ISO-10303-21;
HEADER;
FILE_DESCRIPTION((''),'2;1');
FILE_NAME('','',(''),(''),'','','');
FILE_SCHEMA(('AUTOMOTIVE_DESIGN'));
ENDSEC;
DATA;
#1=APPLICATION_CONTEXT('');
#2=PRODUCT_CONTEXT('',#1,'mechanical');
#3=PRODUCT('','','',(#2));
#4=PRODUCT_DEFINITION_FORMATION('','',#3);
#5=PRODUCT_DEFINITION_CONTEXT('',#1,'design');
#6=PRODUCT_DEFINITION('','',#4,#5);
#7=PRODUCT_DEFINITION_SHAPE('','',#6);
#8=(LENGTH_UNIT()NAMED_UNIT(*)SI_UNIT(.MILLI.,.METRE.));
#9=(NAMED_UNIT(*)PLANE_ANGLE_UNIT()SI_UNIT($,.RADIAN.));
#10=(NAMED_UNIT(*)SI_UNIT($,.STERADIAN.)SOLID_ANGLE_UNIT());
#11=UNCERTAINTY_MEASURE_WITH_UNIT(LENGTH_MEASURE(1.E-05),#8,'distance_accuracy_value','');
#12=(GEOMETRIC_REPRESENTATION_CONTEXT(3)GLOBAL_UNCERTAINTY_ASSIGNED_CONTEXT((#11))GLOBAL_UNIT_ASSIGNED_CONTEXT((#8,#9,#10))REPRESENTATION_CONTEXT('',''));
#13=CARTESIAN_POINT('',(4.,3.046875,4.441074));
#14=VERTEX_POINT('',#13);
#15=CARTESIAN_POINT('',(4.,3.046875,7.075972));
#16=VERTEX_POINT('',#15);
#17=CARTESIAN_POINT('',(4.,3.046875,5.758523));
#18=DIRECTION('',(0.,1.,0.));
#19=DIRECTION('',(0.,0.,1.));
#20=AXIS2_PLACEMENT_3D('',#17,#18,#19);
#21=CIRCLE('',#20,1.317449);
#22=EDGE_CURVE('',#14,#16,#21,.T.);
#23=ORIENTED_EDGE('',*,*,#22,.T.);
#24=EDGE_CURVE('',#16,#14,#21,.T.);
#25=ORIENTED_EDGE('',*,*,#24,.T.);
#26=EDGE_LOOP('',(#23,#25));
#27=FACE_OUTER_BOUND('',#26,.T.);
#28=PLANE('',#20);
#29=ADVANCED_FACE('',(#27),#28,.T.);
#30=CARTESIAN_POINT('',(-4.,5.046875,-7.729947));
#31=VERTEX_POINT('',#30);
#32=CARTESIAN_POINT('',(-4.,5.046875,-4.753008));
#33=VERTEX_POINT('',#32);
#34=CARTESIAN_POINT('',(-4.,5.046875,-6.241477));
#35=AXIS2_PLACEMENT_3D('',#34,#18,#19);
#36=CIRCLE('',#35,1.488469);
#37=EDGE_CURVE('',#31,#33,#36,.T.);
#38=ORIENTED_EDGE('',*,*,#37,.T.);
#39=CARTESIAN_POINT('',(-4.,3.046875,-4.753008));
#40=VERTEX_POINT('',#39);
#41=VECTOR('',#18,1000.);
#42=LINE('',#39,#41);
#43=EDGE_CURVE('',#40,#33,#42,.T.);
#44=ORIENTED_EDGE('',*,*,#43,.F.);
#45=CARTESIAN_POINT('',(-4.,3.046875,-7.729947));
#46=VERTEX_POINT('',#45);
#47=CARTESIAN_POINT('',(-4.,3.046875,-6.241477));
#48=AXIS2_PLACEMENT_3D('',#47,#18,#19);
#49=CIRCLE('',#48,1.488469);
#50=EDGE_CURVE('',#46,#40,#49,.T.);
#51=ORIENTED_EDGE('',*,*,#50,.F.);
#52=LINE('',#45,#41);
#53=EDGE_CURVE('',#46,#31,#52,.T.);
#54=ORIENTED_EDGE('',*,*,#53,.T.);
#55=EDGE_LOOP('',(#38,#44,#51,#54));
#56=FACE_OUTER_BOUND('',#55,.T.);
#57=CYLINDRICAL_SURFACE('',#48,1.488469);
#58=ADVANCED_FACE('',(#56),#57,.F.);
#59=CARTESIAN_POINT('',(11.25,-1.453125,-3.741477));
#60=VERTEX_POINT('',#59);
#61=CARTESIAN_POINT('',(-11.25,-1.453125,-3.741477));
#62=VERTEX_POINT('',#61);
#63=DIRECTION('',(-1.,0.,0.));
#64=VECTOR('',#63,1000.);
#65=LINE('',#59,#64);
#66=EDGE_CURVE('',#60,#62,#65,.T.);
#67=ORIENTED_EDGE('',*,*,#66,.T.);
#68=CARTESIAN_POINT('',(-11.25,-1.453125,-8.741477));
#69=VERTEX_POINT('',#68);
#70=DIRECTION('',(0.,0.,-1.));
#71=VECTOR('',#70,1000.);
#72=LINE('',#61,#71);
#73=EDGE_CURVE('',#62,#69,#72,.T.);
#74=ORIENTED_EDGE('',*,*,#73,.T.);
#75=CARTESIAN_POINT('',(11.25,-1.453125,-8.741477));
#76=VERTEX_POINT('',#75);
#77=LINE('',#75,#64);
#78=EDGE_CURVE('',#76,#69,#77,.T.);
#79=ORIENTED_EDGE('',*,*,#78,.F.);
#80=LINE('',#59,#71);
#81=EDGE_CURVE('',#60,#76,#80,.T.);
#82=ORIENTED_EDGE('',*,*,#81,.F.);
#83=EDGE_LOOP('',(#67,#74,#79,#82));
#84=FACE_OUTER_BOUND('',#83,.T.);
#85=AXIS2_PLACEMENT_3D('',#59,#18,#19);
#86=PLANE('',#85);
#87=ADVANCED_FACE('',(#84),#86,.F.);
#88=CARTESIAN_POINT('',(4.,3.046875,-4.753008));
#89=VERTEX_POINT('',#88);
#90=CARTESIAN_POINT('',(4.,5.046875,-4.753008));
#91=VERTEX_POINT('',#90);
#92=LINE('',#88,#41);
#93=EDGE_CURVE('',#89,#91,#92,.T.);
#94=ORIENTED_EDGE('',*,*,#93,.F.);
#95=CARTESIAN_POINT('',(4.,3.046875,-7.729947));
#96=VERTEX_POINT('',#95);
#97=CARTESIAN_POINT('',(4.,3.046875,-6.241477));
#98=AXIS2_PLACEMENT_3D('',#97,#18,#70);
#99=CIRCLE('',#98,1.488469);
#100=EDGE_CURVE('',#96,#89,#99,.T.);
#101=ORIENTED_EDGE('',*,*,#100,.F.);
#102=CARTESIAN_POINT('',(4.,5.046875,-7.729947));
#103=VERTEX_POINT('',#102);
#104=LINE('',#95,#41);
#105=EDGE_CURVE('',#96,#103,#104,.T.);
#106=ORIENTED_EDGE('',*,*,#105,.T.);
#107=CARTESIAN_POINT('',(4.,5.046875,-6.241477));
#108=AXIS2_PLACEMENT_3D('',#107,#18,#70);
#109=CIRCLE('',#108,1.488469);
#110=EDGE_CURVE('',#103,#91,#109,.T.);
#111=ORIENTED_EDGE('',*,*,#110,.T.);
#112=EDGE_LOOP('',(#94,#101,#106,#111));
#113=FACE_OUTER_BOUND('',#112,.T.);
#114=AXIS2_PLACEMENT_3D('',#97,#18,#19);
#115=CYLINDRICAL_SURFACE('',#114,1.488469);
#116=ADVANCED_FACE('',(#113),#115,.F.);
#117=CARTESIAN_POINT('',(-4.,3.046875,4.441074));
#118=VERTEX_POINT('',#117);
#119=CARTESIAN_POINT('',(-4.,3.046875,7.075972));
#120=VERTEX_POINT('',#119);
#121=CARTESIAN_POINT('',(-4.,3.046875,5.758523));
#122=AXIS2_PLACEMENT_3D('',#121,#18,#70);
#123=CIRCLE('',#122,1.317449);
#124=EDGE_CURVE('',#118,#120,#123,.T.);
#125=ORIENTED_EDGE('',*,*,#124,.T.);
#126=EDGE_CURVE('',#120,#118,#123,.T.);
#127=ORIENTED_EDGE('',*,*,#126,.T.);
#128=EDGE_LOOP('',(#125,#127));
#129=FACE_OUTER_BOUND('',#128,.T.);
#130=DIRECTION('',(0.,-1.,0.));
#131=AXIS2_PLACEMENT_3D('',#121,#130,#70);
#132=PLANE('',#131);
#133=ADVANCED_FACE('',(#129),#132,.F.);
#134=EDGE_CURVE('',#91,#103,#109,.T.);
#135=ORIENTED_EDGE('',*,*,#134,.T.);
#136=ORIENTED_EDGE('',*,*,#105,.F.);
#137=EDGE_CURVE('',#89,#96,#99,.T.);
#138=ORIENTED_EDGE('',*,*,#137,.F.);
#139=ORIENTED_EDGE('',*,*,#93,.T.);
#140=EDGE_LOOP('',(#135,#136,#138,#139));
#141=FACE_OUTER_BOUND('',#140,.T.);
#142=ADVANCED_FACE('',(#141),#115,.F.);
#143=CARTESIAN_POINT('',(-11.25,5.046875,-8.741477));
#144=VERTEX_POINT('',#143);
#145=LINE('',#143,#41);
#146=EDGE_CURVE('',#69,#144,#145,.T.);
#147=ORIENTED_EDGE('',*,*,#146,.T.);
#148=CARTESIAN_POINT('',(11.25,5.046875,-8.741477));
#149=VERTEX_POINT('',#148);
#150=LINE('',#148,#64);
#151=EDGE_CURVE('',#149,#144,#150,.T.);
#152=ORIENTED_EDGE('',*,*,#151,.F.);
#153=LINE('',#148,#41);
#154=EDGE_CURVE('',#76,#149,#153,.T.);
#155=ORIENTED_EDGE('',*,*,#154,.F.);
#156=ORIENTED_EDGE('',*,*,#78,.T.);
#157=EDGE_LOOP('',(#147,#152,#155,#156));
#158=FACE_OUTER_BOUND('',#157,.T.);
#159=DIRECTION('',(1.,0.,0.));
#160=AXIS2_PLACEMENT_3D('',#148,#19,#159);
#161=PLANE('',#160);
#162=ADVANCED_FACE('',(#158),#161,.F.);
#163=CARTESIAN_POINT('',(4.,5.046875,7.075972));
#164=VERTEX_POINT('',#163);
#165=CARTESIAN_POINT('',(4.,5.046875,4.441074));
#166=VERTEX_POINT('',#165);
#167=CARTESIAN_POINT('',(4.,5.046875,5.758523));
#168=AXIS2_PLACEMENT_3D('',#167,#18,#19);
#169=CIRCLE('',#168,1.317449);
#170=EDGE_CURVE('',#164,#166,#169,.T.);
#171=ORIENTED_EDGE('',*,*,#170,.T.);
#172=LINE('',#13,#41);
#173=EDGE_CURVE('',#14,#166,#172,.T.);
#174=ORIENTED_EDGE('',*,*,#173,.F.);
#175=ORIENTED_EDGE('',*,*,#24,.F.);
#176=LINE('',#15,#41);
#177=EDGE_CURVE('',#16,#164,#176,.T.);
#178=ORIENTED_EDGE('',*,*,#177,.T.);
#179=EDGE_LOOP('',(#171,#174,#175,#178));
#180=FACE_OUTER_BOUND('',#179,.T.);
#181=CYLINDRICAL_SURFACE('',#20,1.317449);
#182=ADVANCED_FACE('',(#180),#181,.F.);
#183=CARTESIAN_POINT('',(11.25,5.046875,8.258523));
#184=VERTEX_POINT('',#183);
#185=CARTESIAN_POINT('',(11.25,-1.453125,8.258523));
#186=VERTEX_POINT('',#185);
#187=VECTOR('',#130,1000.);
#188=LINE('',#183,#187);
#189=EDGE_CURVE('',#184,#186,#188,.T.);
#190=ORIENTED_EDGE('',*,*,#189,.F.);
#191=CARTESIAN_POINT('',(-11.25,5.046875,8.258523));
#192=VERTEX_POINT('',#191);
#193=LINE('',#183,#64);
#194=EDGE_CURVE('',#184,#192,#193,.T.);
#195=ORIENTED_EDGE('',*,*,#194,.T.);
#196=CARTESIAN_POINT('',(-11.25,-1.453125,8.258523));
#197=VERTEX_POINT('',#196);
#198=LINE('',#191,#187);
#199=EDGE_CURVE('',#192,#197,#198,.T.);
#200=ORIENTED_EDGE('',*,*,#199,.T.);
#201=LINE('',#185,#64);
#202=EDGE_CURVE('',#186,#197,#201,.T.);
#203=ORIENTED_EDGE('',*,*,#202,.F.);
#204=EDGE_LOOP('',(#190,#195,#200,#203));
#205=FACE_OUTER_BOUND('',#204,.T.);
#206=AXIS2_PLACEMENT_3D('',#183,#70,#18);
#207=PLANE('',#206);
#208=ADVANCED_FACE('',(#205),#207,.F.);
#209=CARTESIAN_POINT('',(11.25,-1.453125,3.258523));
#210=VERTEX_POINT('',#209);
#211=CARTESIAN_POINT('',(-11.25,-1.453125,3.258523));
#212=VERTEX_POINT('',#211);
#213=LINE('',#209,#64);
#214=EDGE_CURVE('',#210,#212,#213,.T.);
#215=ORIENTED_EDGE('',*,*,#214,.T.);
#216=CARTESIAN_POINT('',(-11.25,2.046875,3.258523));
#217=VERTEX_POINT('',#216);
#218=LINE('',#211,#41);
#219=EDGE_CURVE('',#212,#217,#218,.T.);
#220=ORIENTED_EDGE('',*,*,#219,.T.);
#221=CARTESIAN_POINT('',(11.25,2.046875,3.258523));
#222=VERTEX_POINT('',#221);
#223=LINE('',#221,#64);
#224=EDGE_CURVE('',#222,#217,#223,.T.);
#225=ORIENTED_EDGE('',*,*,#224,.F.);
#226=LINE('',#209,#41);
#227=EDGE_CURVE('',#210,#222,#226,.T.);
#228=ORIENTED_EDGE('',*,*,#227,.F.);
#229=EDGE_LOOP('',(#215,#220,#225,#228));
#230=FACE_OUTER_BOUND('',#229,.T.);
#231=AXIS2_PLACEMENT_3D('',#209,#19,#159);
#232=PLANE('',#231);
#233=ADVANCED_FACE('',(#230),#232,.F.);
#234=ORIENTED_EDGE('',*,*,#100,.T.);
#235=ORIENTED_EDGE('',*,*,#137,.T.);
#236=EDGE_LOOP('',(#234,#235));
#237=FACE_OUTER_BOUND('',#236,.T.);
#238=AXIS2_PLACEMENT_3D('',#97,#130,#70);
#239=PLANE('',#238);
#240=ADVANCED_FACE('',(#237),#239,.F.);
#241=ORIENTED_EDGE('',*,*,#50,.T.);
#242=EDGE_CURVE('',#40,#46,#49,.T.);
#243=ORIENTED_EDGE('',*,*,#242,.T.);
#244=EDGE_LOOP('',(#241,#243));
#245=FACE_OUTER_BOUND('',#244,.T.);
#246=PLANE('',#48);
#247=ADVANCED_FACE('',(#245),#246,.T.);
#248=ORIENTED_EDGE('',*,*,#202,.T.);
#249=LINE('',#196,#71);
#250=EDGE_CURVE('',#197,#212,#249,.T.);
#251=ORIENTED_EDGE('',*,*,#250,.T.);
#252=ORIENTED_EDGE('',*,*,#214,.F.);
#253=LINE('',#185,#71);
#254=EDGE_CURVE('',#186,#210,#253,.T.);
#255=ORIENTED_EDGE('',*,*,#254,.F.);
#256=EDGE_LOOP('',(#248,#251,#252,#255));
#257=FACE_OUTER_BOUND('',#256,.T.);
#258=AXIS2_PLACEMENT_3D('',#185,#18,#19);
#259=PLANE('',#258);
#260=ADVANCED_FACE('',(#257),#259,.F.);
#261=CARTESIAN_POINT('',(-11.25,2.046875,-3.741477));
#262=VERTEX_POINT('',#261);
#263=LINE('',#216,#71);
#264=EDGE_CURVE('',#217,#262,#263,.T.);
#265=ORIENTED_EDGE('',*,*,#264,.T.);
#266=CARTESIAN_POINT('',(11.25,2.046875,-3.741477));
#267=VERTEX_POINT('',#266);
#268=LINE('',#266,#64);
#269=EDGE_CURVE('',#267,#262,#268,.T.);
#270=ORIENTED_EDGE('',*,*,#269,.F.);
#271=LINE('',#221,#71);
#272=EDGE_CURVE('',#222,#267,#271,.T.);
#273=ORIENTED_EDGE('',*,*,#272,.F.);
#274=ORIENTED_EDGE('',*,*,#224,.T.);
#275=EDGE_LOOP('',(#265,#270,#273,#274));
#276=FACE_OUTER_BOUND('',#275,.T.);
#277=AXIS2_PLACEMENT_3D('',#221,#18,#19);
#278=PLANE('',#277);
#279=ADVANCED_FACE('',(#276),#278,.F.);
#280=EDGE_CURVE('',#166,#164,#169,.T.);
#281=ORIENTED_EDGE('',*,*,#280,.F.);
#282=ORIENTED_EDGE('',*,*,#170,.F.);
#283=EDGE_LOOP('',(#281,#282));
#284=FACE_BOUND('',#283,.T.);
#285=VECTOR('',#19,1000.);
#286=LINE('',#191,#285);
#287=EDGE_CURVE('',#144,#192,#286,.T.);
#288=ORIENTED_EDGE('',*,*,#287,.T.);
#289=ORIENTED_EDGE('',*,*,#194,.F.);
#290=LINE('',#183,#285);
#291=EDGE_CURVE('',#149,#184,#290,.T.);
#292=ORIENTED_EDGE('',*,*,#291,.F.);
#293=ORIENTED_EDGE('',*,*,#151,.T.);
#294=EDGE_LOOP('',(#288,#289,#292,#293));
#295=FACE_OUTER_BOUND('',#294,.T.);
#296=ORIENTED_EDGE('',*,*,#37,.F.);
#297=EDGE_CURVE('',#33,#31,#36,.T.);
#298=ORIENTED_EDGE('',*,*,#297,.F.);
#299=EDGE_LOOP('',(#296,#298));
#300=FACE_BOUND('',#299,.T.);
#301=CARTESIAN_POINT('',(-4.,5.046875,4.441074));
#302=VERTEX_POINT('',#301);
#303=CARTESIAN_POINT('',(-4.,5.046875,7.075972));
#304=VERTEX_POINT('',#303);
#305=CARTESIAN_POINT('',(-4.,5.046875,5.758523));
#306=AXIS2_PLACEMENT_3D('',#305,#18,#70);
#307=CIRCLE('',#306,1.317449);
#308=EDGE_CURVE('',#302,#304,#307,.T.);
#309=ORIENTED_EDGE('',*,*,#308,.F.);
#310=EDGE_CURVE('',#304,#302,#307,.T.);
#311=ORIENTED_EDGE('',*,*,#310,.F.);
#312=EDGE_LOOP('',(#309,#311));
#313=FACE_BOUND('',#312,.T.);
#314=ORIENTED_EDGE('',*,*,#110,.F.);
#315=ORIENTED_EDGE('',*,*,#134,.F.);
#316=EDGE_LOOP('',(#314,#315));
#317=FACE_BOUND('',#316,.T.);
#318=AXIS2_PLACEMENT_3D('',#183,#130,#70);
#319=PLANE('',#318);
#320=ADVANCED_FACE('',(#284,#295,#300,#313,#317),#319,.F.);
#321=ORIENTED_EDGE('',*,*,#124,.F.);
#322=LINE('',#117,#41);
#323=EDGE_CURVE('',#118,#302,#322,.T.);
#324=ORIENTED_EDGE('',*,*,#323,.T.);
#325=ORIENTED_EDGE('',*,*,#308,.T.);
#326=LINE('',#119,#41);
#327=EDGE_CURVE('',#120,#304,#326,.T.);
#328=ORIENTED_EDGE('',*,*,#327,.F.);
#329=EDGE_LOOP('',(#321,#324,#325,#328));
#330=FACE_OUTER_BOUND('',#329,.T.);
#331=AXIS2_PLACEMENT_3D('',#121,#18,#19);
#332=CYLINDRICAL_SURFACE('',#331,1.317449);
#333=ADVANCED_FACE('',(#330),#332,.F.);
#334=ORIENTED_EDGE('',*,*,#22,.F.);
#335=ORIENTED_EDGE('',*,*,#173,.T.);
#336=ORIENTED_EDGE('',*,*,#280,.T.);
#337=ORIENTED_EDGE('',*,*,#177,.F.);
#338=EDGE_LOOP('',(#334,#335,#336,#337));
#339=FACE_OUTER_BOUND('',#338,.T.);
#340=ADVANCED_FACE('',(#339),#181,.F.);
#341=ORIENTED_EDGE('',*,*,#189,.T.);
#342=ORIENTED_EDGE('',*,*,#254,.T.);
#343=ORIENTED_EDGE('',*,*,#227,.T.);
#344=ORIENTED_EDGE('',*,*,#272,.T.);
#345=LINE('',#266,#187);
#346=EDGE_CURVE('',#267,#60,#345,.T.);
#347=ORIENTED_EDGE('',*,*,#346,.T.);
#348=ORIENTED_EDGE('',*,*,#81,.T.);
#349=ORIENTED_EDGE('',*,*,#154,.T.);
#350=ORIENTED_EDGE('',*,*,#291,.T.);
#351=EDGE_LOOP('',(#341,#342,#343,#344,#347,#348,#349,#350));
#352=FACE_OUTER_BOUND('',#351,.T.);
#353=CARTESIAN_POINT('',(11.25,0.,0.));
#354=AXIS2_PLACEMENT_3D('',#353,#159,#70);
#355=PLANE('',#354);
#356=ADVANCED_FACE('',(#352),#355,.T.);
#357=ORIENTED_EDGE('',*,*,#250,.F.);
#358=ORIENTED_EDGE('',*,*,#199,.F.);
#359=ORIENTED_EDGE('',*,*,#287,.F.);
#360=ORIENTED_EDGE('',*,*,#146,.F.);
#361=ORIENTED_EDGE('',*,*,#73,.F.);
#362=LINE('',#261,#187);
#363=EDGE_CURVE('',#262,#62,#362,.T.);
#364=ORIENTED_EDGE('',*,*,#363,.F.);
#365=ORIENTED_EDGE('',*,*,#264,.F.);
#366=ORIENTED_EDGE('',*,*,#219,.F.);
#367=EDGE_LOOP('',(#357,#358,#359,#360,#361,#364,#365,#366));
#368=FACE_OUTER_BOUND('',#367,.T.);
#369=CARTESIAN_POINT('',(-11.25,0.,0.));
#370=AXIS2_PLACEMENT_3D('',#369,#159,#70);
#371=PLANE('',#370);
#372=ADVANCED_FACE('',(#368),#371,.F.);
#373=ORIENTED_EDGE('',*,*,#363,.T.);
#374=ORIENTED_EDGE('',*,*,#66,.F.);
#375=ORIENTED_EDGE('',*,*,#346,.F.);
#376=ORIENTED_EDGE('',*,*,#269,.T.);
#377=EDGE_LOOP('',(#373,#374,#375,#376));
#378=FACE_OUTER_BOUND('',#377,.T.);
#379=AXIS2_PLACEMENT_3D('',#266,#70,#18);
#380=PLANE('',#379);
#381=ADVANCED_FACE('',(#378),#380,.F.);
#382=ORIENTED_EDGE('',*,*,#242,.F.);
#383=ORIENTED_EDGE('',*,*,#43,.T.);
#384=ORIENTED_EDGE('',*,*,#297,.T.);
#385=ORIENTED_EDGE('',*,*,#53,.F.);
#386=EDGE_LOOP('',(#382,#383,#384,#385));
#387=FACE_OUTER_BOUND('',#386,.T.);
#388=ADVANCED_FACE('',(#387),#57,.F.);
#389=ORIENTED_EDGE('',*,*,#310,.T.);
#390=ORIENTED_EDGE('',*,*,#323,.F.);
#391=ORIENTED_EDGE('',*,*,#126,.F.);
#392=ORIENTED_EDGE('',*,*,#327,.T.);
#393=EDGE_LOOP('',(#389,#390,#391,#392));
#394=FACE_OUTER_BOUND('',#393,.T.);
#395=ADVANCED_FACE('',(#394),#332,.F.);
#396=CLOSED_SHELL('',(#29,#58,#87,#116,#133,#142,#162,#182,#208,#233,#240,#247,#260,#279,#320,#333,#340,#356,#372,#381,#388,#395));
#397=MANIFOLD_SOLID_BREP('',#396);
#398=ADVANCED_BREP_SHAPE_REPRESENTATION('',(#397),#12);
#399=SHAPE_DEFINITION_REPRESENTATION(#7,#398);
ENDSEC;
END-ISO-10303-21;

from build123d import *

# Parameters (mm, degrees)
BOSS_EXTRUDE1_DEPTH = 11.25
SKETCH2_R           = 1.317449136
SKETCH2_R_2         = 1.488469479
CUT_EXTRUDE1_DEPTH  = 2


with BuildPart() as part:
    # Sketch1 → Boss-Extrude1 (new, symmetric)
    with BuildSketch(Plane(origin=(0, 0, 0), x_dir=(0, 0, -1), z_dir=(1, 0, 0))):
        Polygon((-8.258522727, 5.046875), (8.741477273, 5.046875), (8.741477273, -1.453125), (3.741477273, -1.453125), (3.741477273, 2.046875), (-3.258522727, 2.046875), (-3.258522727, -1.453125), (-8.258522727, -1.453125), align=None)
    extrude(amount=BOSS_EXTRUDE1_DEPTH, both=True)

    # Sketch2 → Cut-Extrude1 (cut)
    with BuildSketch(Plane(origin=(0, 5.046875, 0), x_dir=(1, 0, 0), z_dir=(0, 1, 0))):
        with Locations(Location((4, -5.758522727, 0), (0, 0, 270))):
            Circle(SKETCH2_R)
        with Locations(Location((-4, 6.241477273, 0), (0, 0, 270))):
            Circle(SKETCH2_R_2)
        with Locations(Location((4, 6.241477273, 0), (0, 0, 90))):
            Circle(SKETCH2_R_2)
        with Locations(Location((-4, -5.758522727, 0), (0, 0, 90))):
            Circle(SKETCH2_R)
    extrude(amount=-CUT_EXTRUDE1_DEPTH, mode=Mode.SUBTRACT)


solid = part.part
